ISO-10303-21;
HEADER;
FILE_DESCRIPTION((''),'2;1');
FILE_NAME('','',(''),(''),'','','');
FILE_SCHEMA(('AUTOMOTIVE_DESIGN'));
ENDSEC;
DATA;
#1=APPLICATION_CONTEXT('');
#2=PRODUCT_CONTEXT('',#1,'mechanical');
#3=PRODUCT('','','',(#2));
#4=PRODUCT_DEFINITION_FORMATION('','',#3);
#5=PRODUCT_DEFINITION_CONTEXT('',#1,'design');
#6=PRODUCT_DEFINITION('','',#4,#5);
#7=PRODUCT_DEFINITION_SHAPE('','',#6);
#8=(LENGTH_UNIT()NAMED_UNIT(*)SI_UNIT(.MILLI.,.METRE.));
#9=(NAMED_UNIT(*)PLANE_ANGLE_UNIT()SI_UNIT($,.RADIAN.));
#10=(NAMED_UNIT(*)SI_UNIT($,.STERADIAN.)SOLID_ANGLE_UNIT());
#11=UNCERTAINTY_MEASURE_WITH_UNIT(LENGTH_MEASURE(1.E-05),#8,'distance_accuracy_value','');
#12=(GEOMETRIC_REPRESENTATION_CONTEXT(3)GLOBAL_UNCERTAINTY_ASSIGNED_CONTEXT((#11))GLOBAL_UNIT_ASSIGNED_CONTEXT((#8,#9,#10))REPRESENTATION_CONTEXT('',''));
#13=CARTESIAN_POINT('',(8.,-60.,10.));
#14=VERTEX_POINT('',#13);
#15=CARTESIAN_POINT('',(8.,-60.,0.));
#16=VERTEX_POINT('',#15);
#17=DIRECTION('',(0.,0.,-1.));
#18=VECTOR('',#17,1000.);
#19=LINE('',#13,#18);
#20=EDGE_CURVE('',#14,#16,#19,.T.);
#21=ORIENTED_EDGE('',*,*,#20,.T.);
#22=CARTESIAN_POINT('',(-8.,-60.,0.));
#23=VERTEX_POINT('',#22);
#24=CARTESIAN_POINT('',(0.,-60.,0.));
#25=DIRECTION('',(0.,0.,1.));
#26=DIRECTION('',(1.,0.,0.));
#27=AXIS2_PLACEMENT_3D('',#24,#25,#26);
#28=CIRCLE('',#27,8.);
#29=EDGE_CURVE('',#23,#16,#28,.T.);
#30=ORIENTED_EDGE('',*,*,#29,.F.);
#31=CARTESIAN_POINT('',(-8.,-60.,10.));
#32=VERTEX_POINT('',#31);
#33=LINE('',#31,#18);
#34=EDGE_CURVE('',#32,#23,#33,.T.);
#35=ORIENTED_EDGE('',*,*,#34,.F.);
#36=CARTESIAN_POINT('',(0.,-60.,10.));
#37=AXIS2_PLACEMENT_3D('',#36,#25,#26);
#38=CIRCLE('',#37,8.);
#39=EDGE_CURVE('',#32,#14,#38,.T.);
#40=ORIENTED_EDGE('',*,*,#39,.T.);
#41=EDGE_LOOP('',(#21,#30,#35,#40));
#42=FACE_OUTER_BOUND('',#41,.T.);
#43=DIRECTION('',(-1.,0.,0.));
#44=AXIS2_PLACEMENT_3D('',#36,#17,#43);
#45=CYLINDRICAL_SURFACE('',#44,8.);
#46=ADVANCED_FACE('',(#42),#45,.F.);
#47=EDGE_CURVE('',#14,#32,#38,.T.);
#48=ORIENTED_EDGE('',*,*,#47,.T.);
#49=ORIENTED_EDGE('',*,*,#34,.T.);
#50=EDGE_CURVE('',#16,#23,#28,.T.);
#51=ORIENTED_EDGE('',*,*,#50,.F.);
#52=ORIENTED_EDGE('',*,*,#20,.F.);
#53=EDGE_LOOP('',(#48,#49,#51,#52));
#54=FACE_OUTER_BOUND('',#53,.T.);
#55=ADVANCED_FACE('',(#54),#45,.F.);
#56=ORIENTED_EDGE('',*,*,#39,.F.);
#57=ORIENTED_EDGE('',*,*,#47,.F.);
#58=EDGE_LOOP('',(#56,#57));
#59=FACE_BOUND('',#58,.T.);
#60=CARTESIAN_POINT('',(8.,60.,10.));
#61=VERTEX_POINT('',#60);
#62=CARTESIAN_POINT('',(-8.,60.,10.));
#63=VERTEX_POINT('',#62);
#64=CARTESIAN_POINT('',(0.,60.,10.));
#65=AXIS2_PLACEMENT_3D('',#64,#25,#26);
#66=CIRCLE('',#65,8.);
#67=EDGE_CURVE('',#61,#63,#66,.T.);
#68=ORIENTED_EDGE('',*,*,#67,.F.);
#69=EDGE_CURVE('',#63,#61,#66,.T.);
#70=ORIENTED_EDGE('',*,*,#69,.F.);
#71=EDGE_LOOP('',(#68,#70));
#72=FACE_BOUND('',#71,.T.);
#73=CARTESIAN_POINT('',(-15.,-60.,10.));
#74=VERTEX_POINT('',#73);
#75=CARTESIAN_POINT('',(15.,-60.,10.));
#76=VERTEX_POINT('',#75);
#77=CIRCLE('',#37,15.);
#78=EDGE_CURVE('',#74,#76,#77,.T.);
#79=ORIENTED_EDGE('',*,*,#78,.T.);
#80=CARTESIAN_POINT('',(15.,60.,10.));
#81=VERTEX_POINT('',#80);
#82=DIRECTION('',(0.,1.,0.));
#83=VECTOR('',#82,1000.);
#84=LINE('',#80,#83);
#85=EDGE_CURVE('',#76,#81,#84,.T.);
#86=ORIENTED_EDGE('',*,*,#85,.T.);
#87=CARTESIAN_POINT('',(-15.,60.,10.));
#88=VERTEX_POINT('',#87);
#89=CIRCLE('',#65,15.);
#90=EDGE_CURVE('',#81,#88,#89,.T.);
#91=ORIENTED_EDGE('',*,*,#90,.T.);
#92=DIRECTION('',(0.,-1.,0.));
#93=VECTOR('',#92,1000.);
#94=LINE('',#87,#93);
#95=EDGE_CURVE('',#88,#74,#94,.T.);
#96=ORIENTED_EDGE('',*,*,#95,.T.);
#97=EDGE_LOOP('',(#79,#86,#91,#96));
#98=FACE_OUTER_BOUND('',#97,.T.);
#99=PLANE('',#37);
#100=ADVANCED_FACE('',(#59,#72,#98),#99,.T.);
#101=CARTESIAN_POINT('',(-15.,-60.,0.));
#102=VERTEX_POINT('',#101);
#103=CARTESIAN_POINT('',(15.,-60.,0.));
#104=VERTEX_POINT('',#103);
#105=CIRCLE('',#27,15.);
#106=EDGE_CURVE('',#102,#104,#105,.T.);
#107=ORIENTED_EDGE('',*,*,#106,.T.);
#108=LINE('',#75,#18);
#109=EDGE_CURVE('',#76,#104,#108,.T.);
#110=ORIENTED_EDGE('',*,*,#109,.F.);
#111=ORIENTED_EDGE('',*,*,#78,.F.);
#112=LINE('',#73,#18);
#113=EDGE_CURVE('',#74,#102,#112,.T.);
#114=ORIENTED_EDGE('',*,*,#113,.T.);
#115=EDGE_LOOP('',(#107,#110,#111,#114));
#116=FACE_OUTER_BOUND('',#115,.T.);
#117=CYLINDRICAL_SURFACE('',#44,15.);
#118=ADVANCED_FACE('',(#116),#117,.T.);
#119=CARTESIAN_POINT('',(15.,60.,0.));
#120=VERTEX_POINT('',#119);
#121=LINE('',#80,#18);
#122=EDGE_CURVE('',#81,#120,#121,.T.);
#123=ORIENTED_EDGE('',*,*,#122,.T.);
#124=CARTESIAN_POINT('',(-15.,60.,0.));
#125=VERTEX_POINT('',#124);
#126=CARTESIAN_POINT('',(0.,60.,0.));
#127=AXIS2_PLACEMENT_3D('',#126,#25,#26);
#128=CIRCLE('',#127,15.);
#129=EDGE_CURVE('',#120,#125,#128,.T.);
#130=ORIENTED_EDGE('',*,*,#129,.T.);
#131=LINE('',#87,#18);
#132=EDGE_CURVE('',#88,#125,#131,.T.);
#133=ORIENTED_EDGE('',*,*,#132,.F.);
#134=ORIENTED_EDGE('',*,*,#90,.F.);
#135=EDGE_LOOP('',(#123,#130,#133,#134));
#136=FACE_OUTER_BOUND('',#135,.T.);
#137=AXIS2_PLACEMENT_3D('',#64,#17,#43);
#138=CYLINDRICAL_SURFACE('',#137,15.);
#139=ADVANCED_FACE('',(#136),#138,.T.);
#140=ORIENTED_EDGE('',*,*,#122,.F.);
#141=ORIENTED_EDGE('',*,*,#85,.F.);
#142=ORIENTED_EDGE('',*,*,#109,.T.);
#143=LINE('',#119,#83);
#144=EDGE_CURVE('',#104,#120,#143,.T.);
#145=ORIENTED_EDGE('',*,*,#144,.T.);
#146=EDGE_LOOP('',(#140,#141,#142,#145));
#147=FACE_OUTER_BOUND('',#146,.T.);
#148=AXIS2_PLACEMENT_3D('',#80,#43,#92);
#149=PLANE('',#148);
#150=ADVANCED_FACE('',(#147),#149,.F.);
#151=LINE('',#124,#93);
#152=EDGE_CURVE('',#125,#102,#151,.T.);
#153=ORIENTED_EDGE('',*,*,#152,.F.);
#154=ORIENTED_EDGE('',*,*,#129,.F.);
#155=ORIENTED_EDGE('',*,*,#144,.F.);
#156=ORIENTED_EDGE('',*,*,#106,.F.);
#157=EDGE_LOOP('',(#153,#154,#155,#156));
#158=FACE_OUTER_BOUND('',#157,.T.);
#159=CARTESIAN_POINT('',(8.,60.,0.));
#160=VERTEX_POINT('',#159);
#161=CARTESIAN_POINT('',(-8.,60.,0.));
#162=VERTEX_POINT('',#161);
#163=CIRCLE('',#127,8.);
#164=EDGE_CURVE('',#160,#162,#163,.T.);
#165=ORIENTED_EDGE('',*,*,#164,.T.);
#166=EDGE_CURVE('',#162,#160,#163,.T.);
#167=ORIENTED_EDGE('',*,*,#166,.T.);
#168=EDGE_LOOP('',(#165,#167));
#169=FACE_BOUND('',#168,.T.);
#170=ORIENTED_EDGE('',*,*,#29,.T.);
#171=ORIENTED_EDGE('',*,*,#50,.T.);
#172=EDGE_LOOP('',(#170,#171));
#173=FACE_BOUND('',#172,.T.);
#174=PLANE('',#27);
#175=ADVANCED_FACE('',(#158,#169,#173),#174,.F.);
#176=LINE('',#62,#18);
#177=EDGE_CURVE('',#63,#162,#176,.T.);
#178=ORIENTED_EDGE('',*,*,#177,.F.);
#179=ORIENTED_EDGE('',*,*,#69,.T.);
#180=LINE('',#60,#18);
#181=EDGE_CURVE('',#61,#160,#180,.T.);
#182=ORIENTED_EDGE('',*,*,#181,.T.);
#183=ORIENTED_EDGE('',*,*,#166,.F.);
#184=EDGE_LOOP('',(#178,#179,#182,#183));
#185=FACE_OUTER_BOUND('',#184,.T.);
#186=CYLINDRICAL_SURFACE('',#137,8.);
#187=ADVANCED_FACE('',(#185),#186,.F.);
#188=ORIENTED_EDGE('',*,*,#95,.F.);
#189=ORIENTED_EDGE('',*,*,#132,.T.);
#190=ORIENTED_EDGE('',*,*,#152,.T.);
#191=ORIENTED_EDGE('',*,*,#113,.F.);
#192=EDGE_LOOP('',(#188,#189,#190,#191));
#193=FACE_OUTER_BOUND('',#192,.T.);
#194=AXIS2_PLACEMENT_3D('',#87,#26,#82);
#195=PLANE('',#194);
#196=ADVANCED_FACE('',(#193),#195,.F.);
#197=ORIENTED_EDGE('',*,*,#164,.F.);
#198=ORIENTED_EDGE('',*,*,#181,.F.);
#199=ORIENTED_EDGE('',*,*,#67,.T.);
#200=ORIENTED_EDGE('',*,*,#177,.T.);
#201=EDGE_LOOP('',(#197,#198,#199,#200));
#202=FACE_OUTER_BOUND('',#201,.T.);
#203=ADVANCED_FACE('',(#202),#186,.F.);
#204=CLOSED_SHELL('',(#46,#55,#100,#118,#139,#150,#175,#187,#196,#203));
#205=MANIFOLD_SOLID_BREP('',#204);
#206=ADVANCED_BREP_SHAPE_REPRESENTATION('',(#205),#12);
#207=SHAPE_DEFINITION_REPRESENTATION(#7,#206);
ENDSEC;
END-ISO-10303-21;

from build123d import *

# Parameters (mm, degrees)
SKETCH1_R           = 8
BOSS_EXTRUDE1_DEPTH = 10


with BuildPart() as part:
    # Sketch1 → Boss-Extrude1 (new body)
    with BuildSketch(Plane.XY):
        with BuildLine():
            Line((-15, 60), (-15, -60))
            ThreePointArc((-15, -60), (0, -75), (15, -60))
            Line((15, -60), (15, 60))
            ThreePointArc((15, 60), (0, 75), (-15, 60))
        make_face()
        with Locations((0, 60)):
            Circle(SKETCH1_R, mode=Mode.SUBTRACT)
        with Locations((0, -60)):
            Circle(SKETCH1_R, mode=Mode.SUBTRACT)
    extrude(amount=BOSS_EXTRUDE1_DEPTH)


solid = part.part
